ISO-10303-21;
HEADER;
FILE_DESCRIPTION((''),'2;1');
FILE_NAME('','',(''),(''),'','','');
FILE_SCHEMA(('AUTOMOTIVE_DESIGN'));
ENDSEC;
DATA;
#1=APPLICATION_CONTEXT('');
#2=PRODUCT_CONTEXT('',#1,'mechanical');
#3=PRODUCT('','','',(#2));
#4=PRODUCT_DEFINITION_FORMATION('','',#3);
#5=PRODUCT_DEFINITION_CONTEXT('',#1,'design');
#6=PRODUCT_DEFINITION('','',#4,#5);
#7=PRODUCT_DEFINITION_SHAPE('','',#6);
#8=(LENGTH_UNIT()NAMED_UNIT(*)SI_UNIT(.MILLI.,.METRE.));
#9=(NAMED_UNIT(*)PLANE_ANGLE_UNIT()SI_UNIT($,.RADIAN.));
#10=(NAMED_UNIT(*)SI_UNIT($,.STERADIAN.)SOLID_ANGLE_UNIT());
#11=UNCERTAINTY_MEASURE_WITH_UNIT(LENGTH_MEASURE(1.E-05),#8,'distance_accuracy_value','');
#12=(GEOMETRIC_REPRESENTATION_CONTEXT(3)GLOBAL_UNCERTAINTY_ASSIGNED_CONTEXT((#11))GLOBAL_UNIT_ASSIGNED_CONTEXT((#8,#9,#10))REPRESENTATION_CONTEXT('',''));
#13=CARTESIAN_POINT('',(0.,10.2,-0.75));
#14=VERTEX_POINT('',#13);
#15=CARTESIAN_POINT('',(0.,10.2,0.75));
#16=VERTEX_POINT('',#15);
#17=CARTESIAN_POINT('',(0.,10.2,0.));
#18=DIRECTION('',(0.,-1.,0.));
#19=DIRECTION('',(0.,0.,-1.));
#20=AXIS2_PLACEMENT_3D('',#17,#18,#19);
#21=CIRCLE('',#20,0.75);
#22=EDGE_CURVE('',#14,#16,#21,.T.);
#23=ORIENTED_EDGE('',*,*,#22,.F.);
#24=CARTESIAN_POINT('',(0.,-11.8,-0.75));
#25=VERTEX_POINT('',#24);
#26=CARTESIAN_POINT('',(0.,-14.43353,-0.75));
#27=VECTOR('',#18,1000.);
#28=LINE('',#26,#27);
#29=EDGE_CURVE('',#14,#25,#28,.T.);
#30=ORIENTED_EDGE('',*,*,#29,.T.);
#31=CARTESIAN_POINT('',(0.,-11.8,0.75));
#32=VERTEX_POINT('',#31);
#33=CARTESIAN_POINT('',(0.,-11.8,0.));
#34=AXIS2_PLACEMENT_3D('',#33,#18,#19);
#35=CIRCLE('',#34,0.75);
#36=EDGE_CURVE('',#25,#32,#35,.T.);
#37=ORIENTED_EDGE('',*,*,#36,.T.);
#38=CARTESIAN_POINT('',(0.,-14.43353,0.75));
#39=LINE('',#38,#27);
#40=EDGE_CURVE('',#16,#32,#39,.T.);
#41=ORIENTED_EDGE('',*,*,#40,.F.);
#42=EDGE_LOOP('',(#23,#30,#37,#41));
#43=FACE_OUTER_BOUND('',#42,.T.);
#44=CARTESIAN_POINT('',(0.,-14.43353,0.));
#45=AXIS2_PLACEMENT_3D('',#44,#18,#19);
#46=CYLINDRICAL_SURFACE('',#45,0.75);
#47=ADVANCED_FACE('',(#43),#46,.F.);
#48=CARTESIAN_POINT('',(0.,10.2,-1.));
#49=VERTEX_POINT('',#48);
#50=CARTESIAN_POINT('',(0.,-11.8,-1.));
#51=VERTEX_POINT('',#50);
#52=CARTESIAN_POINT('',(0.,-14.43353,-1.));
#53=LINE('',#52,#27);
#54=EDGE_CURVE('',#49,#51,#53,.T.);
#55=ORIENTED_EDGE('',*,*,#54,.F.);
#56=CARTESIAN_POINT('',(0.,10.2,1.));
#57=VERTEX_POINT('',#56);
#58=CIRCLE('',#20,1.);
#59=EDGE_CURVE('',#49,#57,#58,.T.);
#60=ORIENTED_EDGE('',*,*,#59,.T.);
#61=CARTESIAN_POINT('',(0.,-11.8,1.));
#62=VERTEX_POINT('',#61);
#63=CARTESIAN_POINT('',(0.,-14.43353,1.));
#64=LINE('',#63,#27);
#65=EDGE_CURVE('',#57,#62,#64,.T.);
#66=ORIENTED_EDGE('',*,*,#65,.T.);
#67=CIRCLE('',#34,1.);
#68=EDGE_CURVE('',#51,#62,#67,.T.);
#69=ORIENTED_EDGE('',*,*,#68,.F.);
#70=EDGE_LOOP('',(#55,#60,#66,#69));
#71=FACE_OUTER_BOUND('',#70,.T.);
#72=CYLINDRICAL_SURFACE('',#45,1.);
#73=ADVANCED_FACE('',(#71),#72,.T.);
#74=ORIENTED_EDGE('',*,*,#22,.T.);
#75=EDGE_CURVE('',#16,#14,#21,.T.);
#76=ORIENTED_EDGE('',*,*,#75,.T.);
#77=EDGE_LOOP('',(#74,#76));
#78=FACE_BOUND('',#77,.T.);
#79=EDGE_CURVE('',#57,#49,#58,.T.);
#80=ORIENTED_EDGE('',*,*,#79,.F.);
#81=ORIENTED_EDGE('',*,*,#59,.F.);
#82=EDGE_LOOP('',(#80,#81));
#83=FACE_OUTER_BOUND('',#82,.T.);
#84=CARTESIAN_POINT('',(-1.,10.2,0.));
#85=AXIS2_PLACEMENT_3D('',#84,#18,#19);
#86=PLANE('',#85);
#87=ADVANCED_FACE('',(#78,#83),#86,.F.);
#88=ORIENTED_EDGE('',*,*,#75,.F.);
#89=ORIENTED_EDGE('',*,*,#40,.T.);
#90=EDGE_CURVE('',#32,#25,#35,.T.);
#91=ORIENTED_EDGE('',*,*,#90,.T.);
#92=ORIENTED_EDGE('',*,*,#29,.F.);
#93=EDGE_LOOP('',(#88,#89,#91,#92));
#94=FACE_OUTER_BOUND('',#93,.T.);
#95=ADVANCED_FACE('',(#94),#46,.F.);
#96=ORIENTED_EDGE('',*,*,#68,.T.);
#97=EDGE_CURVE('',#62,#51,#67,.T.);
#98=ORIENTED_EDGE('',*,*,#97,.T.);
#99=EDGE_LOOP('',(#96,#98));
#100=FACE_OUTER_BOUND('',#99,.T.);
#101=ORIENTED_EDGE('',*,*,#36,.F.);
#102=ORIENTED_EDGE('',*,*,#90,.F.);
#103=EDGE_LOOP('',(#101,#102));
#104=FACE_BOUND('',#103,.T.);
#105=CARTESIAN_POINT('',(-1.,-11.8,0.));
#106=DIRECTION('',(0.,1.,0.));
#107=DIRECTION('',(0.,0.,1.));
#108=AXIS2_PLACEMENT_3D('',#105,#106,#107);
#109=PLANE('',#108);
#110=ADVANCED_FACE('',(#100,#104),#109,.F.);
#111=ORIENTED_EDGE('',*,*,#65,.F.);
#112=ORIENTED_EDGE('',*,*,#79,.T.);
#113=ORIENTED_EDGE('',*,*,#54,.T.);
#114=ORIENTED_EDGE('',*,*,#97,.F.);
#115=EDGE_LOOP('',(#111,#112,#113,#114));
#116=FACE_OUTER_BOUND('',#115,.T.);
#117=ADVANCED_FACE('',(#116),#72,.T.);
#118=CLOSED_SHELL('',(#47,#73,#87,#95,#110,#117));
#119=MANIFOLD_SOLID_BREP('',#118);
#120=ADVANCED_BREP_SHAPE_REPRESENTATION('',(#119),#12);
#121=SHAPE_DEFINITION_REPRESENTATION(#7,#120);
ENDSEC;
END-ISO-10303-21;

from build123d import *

# Parameters (mm, degrees)
SKETCH1_W = 0.25
SKETCH1_H = 22


with BuildPart() as part:
    # Sketch1 → Revolve1 (revolve)
    with BuildSketch(Plane.XY, mode=Mode.PRIVATE) as revolve1_sk:
        with Locations((-0.875, -0.8)):
            Rectangle(SKETCH1_W, SKETCH1_H)
    revolve(revolve1_sk.sketch.rotate(Axis((0, -14.433529877, 0), (0, 1, 0)), 270), axis=Axis((0, -14.433529877, 0), (0, 1, 0)))


solid = part.part
